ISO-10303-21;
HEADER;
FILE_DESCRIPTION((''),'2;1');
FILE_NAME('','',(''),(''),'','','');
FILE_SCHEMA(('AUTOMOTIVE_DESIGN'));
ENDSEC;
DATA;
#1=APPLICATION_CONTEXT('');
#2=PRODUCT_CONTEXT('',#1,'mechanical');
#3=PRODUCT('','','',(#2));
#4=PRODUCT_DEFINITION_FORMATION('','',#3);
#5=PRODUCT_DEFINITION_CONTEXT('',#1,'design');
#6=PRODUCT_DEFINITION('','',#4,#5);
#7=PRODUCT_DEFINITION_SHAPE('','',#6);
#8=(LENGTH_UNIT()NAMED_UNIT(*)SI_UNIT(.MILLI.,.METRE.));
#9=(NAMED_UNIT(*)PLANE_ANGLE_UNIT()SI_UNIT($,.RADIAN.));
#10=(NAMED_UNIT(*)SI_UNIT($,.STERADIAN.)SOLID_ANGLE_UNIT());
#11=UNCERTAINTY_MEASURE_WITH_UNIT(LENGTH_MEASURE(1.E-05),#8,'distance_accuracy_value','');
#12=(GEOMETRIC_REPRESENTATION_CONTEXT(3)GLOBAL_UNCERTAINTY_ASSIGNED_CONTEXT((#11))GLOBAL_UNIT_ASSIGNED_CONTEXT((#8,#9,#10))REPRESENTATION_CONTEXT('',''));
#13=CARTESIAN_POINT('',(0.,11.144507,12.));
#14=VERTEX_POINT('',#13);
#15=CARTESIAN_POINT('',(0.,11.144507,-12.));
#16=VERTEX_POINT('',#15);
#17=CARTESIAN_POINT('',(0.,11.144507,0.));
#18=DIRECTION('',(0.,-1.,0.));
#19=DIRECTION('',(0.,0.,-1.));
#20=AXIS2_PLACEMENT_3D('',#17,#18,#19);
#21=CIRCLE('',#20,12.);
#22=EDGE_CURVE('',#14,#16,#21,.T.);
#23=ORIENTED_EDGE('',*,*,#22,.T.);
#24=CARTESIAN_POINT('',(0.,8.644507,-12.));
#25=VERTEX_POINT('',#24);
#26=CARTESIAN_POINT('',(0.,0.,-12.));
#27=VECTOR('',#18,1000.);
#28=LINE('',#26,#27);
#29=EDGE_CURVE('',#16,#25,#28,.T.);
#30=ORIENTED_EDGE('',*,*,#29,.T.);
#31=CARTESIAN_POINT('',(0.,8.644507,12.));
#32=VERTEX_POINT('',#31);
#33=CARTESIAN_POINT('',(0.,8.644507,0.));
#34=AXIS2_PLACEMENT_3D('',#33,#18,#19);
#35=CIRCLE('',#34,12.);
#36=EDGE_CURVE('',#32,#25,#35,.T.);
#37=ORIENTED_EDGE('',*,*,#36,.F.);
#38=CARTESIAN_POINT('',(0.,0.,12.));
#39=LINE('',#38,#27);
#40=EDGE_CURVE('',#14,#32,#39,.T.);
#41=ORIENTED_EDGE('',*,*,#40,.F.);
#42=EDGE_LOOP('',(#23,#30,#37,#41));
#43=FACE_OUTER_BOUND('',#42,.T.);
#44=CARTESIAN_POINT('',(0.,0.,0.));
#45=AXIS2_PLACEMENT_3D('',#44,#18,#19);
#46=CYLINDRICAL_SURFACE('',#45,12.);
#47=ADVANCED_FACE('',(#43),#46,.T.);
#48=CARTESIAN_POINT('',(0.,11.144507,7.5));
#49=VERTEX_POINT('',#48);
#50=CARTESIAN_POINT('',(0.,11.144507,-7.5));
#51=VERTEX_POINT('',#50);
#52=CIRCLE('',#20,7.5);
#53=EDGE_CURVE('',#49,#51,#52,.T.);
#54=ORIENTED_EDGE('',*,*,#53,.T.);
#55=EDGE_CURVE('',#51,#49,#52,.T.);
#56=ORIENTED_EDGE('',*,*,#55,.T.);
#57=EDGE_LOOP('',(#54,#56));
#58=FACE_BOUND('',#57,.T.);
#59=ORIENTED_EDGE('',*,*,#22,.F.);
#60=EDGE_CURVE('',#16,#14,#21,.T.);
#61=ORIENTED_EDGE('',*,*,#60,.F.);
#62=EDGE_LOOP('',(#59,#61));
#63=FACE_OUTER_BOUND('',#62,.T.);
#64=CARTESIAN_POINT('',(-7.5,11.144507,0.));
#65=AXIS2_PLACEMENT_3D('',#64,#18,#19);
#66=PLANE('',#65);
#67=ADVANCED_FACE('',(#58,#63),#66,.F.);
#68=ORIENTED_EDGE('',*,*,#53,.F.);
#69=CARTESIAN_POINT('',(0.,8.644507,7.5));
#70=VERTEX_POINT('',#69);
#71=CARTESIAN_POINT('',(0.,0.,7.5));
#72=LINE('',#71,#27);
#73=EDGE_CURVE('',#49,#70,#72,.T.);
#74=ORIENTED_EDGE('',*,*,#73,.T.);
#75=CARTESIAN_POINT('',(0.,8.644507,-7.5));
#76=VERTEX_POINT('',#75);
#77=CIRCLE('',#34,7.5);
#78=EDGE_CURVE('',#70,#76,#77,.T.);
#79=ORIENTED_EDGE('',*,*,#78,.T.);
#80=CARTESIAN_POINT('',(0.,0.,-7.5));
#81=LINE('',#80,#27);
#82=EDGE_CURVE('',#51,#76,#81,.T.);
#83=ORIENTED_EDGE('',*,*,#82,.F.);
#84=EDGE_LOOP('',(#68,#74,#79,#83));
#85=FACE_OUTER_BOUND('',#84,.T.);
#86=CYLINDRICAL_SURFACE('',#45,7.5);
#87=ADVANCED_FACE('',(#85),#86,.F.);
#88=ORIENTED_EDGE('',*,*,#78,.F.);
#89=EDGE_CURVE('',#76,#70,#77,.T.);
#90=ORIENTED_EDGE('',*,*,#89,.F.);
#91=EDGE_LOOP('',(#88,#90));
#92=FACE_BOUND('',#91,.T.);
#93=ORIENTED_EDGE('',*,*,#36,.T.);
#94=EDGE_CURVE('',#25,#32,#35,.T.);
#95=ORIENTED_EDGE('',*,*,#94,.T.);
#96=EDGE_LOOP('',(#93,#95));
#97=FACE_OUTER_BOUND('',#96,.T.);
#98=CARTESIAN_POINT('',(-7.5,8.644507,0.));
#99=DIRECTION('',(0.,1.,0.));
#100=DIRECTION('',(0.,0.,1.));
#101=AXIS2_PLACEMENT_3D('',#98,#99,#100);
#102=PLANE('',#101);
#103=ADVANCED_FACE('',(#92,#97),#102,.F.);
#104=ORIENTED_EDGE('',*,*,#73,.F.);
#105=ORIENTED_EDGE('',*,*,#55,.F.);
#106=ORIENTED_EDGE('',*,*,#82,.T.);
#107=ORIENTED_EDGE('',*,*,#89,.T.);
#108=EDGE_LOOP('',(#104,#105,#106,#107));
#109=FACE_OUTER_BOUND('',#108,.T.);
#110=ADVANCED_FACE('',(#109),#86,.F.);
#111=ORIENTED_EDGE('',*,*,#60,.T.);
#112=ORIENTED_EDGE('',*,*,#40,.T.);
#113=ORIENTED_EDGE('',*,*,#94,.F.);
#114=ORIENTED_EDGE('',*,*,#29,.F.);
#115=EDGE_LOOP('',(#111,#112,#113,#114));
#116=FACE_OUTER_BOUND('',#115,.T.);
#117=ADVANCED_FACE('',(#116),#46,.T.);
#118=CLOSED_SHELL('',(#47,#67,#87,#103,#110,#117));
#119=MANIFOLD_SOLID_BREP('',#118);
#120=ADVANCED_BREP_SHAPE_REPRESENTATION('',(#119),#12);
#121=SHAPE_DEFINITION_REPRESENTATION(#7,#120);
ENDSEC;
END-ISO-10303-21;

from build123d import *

# Parameters (mm, degrees)
SKETCH1_W = 4.5
SKETCH1_H = 2.5


with BuildPart() as part:
    # Sketch1 → Boss-Revolve (revolve)
    with BuildSketch(Plane.XY, mode=Mode.PRIVATE) as boss_revolve_sk:
        with Locations((-9.75, 9.894507042)):
            Rectangle(SKETCH1_W, SKETCH1_H)
    revolve(boss_revolve_sk.sketch.rotate(Axis((0, 0, 0), (0, 1, 0)), 270), axis=Axis((0, 0, 0), (0, 1, 0)))


solid = part.part
